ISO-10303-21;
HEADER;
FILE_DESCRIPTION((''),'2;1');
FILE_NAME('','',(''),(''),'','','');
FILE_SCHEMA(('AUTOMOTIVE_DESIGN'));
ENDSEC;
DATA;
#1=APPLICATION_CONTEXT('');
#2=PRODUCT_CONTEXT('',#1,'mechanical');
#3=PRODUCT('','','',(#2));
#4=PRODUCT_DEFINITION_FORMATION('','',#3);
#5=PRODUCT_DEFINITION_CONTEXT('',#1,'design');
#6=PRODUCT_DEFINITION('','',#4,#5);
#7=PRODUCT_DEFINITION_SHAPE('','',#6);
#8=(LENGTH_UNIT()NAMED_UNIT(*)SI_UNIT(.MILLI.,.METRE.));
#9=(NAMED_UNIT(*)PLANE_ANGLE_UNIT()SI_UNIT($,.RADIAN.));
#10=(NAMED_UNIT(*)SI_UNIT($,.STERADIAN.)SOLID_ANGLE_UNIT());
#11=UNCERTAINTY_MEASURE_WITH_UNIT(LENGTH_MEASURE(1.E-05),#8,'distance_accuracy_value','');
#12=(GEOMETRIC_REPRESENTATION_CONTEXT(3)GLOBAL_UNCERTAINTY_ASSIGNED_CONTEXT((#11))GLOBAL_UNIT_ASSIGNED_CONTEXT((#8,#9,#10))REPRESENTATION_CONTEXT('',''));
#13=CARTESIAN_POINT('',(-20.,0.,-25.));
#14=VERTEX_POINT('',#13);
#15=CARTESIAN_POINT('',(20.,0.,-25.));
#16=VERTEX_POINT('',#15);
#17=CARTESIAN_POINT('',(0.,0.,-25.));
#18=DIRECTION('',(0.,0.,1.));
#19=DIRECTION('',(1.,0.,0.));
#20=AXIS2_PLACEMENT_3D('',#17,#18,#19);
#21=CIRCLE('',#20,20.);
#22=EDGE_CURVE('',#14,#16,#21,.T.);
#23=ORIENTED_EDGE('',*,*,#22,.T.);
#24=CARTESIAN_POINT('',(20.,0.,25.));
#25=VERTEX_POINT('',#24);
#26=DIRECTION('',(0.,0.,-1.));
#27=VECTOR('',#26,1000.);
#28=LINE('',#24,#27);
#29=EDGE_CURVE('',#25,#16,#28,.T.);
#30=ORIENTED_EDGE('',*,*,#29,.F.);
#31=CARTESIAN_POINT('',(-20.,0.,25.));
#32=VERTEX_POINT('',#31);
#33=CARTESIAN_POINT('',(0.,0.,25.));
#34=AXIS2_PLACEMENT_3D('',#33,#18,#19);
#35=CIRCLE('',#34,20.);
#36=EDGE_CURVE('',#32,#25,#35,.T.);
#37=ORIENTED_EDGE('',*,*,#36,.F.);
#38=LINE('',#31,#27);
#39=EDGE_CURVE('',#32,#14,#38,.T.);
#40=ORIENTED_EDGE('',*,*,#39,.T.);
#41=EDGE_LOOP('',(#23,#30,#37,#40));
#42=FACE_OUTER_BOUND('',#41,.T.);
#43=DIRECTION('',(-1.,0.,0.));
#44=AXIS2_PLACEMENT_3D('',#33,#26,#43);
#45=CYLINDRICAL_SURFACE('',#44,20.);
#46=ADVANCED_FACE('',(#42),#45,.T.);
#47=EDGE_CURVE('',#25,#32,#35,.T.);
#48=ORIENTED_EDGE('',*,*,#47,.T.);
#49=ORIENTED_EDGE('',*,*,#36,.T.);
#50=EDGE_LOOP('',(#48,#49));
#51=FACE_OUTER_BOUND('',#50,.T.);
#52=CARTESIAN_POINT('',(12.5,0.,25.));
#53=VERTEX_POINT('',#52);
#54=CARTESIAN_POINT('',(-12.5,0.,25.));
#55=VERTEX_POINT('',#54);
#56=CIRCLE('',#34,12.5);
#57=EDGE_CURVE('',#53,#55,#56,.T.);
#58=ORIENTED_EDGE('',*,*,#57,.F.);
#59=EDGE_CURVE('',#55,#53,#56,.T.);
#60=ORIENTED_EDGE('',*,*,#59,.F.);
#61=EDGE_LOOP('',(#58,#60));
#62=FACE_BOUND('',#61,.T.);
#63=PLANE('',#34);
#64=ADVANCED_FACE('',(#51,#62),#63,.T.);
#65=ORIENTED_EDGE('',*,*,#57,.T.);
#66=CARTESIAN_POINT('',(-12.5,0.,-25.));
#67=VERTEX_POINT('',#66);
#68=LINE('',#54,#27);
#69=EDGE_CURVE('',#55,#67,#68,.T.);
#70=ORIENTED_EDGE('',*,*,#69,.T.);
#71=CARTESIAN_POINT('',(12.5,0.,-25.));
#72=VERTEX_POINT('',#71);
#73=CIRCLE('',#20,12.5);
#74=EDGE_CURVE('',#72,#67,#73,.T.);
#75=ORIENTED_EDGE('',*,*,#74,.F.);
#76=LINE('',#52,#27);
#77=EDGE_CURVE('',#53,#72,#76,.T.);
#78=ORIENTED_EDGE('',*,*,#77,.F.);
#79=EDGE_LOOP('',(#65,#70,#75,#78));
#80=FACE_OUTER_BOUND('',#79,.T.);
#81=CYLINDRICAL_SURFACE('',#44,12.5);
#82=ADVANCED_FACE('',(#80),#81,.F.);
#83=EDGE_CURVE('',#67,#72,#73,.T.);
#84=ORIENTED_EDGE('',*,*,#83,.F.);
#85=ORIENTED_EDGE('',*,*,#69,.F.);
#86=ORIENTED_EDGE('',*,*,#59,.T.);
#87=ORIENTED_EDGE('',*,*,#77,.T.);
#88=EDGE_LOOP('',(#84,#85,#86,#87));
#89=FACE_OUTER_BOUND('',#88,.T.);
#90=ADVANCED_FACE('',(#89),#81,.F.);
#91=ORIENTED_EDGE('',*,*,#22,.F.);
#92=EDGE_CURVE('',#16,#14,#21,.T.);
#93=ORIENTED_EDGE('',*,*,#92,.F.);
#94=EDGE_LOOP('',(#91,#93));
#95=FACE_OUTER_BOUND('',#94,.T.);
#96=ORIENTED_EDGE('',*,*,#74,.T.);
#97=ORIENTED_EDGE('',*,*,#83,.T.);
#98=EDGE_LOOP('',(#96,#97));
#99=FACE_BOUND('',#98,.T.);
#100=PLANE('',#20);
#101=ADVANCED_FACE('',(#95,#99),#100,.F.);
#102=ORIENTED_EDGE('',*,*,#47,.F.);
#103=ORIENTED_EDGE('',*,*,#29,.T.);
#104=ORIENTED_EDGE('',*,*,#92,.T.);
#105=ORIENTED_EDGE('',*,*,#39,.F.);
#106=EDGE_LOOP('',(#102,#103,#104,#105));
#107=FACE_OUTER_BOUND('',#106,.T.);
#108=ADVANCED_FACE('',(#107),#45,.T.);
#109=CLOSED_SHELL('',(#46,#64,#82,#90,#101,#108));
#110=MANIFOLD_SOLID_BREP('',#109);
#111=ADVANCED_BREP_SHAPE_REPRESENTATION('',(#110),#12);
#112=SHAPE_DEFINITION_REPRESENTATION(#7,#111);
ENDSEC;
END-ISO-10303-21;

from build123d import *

# Parameters (mm, degrees)
SKETCH_1_R      = 20
SKETCH_1_R_2    = 12.5
EXTRUDE_1_DEPTH = 25


with BuildPart() as part:
    # 草图1 → 凸台-拉伸1 (new, symmetric)
    with BuildSketch(Plane.XY):
        Circle(SKETCH_1_R)
        Circle(SKETCH_1_R_2, mode=Mode.SUBTRACT)
    extrude(amount=EXTRUDE_1_DEPTH, both=True)


solid = part.part
